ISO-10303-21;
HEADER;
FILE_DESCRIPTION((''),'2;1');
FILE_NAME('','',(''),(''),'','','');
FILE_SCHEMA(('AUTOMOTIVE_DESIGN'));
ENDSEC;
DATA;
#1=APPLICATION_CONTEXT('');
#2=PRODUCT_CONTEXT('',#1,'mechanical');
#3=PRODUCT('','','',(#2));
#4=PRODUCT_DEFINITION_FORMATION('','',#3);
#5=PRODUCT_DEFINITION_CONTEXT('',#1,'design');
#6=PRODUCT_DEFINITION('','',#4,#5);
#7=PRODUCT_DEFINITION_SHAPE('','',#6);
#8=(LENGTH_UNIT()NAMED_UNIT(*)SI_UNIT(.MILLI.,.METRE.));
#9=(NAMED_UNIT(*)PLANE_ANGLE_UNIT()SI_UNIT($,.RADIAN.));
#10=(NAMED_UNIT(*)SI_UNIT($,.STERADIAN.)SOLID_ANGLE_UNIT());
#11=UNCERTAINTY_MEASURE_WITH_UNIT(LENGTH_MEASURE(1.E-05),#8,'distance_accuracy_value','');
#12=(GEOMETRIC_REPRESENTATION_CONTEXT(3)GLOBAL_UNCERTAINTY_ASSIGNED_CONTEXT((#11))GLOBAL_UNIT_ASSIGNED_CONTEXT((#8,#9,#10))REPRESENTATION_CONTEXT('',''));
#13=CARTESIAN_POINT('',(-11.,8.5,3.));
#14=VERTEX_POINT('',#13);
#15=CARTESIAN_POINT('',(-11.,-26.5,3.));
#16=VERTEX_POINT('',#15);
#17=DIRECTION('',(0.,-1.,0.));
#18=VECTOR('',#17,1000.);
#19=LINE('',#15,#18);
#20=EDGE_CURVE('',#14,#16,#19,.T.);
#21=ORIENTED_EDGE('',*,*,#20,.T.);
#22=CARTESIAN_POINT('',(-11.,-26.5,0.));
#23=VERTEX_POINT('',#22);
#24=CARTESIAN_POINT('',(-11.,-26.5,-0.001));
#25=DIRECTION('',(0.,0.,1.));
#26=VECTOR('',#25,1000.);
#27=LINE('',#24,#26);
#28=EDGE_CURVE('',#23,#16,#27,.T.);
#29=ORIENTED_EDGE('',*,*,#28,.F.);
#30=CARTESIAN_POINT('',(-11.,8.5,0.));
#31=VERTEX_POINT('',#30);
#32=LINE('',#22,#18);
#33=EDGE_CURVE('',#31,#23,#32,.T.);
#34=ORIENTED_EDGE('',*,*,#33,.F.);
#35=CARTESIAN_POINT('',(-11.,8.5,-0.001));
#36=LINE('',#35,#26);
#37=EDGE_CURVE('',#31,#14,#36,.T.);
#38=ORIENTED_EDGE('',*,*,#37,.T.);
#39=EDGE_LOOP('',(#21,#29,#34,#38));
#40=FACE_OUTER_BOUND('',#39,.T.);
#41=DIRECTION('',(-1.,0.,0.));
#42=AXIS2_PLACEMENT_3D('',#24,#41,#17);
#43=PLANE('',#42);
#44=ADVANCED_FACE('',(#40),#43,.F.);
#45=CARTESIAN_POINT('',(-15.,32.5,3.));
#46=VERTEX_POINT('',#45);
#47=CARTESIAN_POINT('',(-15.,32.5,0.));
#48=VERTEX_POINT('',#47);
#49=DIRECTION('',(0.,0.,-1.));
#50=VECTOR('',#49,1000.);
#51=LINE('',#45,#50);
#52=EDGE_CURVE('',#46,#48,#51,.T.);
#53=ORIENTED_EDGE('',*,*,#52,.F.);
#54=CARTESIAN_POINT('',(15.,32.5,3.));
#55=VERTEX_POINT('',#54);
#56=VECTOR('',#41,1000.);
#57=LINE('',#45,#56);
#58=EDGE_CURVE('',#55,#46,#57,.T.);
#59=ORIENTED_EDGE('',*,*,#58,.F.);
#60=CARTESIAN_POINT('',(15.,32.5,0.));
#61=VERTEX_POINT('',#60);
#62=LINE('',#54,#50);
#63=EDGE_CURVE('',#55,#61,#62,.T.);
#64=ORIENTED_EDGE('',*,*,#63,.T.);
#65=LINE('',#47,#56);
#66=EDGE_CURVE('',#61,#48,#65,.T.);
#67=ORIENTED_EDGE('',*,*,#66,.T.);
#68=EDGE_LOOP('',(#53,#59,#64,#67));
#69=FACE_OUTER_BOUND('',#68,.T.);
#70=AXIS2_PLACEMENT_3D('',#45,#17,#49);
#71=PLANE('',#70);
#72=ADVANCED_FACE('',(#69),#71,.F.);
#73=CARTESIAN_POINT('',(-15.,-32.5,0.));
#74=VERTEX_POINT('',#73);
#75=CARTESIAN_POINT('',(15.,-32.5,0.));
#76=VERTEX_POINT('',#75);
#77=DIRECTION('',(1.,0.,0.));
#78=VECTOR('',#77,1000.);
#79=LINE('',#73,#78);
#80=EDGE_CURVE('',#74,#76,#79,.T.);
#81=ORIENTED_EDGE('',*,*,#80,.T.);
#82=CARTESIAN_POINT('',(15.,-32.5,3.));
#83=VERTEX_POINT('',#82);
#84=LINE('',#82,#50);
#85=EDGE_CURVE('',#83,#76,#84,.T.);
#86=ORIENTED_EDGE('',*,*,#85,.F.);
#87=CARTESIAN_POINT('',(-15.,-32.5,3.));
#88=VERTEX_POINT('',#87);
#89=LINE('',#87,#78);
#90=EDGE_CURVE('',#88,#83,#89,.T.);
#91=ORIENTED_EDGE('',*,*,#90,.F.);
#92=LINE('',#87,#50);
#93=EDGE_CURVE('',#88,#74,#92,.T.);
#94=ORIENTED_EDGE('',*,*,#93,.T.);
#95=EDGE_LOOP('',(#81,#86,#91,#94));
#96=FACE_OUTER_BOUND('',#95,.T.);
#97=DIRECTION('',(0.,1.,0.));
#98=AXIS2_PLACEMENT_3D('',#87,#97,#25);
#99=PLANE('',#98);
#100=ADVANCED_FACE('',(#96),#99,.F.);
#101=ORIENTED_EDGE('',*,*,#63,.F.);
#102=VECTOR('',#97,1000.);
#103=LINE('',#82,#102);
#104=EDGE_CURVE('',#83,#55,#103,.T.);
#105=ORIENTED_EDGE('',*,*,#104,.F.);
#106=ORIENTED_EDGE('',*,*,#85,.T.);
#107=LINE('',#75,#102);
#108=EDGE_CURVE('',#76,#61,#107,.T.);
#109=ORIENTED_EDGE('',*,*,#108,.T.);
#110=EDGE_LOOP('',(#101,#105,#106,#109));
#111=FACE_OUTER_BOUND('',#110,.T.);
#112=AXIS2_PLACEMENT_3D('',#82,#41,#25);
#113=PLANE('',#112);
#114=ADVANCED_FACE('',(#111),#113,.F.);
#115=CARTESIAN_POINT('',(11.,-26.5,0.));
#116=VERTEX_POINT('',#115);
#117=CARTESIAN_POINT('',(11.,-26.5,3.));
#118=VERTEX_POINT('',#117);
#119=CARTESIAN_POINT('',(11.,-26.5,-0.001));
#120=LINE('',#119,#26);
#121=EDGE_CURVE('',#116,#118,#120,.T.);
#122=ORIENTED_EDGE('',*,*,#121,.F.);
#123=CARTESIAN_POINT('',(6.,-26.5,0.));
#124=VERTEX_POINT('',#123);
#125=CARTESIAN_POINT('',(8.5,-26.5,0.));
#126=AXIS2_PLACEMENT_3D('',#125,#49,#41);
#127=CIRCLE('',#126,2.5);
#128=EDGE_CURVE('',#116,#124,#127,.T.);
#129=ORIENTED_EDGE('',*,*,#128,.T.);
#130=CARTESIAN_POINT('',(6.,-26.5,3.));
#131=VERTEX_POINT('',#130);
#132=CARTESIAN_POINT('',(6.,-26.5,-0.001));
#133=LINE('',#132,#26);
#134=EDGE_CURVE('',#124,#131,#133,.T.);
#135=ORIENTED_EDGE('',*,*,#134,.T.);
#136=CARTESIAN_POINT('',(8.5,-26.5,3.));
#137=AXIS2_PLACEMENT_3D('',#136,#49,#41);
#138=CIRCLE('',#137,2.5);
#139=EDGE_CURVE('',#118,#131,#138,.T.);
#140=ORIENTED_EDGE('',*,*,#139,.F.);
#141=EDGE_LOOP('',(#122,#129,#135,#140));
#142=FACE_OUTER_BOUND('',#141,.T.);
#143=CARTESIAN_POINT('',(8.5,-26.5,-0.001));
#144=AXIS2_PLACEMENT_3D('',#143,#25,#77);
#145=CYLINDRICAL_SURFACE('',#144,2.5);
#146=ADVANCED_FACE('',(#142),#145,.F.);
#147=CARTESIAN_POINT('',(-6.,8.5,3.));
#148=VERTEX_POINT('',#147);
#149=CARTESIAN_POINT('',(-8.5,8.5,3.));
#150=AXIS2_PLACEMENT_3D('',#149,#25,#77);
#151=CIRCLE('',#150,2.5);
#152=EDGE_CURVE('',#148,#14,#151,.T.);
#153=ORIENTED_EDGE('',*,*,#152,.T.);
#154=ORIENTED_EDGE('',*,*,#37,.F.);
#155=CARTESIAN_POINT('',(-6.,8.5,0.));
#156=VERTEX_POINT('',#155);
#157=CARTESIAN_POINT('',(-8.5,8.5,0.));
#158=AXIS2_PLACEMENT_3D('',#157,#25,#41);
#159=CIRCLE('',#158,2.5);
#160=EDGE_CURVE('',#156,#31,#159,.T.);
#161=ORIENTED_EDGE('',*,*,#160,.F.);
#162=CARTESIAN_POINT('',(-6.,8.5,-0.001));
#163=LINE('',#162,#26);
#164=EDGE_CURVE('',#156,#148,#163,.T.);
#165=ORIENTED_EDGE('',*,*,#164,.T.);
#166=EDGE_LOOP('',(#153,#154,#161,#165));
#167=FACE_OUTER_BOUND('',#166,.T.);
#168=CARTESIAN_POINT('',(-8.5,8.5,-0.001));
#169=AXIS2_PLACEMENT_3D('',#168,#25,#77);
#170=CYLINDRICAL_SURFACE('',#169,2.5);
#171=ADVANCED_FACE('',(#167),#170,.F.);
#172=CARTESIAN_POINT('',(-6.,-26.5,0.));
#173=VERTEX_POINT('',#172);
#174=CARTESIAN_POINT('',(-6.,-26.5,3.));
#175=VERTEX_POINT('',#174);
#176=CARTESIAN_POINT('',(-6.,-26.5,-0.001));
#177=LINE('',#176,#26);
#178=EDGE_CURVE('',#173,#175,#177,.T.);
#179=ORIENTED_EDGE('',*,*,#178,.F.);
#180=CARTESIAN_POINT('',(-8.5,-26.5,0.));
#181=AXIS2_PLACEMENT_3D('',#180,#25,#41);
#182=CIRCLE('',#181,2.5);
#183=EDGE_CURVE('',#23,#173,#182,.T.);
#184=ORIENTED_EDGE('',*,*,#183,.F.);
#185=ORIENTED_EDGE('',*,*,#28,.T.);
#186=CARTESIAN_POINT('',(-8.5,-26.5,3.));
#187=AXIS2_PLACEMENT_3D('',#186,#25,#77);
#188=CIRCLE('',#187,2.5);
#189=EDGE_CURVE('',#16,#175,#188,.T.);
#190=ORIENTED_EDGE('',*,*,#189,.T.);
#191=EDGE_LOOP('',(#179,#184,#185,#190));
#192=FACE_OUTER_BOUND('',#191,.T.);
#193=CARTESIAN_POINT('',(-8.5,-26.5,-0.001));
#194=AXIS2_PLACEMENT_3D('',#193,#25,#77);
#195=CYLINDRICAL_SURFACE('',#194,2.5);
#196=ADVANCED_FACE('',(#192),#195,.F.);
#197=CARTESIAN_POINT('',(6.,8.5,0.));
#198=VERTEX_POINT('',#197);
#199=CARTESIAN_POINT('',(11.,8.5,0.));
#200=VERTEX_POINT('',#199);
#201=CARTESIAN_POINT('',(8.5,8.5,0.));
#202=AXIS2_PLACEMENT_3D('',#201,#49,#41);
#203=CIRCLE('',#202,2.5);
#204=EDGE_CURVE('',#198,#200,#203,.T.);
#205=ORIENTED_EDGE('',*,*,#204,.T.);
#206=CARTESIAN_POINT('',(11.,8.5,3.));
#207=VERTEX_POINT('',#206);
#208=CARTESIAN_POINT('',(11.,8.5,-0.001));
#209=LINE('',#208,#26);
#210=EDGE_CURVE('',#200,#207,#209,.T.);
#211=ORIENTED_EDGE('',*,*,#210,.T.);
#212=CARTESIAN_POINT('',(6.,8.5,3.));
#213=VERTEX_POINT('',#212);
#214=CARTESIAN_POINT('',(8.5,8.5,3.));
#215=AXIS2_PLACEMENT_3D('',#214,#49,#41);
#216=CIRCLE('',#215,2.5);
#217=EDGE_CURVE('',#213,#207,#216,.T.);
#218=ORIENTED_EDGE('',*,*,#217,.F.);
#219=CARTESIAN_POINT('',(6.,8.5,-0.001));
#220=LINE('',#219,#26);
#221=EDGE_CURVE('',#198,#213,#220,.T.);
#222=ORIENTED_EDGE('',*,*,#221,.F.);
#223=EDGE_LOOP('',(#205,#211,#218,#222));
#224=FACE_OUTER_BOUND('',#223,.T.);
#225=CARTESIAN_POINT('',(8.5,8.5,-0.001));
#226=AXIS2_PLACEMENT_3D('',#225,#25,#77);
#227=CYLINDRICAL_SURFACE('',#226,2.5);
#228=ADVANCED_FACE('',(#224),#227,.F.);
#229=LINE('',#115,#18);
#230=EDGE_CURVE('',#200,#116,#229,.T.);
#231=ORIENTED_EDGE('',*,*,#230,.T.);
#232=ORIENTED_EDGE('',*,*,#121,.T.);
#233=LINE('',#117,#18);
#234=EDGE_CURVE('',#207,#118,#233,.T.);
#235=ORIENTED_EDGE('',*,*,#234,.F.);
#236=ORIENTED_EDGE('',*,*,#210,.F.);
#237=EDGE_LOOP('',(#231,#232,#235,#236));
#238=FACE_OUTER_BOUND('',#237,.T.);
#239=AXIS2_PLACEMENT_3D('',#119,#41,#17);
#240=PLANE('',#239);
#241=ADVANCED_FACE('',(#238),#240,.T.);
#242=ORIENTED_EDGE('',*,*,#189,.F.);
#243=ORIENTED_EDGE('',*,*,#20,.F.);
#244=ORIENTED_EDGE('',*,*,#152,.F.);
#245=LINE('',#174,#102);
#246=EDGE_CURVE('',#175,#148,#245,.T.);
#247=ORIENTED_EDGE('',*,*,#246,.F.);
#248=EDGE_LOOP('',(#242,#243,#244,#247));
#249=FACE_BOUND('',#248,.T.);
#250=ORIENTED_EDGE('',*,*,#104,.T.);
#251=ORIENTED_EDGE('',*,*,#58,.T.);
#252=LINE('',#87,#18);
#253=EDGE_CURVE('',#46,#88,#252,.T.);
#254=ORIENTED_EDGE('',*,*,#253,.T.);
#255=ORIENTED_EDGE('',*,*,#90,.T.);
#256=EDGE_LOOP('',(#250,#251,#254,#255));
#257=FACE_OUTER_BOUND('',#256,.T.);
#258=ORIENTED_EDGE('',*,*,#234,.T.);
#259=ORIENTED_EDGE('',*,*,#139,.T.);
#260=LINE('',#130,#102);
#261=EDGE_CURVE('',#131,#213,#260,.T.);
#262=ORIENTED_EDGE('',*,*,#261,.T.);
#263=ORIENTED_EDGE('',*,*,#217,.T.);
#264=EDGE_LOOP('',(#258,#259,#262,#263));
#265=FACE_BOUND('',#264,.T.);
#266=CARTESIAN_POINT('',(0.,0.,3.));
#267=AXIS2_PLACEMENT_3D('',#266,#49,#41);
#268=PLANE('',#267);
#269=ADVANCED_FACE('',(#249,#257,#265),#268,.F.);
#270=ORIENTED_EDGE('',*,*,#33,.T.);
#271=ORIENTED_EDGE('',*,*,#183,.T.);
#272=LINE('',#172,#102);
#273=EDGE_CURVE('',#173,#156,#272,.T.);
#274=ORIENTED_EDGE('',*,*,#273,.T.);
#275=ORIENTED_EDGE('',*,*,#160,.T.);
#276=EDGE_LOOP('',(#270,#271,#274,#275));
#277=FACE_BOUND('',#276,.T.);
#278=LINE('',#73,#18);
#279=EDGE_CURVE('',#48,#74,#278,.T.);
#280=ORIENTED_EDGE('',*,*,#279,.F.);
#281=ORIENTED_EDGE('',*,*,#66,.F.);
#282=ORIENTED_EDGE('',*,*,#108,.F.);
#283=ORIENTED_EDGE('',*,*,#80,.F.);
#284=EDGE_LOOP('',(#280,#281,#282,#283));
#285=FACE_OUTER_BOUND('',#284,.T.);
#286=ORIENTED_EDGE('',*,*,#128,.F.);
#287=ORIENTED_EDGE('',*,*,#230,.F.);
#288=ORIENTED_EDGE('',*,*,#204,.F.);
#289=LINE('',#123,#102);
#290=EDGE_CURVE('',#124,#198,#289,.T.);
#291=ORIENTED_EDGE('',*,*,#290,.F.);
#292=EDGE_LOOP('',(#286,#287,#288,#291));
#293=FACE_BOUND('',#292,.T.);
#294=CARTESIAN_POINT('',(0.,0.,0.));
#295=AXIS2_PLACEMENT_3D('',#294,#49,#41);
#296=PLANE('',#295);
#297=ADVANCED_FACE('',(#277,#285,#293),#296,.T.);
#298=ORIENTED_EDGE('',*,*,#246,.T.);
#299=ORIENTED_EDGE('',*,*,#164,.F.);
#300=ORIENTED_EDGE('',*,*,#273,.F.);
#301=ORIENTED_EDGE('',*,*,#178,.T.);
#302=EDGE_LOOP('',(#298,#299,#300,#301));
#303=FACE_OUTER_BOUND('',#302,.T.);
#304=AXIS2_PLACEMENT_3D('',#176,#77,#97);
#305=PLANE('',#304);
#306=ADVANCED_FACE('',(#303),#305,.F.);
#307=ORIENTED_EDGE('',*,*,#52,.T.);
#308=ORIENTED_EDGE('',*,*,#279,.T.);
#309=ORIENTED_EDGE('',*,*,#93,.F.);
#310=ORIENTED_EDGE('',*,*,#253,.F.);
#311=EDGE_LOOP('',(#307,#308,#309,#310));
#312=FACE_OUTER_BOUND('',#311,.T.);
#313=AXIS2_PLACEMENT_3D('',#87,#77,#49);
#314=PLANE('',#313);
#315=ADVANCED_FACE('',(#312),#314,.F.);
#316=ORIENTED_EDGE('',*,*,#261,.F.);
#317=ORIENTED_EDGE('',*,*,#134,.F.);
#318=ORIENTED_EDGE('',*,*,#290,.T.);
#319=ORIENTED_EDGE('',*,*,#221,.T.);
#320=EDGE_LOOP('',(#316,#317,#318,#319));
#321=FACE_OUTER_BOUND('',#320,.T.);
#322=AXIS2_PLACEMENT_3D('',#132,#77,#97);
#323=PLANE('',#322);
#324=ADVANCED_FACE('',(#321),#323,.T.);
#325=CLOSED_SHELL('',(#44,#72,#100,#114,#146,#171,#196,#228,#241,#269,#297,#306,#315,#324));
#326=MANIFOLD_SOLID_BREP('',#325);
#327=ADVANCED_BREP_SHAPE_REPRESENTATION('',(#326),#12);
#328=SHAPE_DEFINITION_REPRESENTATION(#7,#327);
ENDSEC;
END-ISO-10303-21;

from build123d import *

# Parameters (mm, degrees)
SKETCH_1_W          = 30
SKETCH_1_H          = 65
EXTRUDE_1_DEPTH     = 3
CUT_EXTRUDE_1_REACH = 37.92


with BuildPart() as part:
    # 草图1 → 凸台-拉伸1 (new body)
    with BuildSketch(Plane.XY):
        Rectangle(SKETCH_1_W, SKETCH_1_H)
    extrude(amount=EXTRUDE_1_DEPTH)

    # 草图2 → 切除-拉伸1 (cut, up to next)
    with BuildSketch(Plane.XY.offset(3), mode=Mode.PRIVATE) as cut_extrude_1_sk1:
        with BuildLine():
            Line((-11, -26.5), (-11, 8.5))
            ThreePointArc((-11, 8.5), (-8.5, 11), (-6, 8.5))
            Line((-6, 8.5), (-6, -26.5))
            ThreePointArc((-6, -26.5), (-8.5, -29), (-11, -26.5))
        make_face()
    cut_extrude_1_tool1 = extrude(cut_extrude_1_sk1.sketch, amount=-CUT_EXTRUDE_1_REACH, mode=Mode.PRIVATE) & part.part
    cut_extrude_1 = cut_extrude_1_tool1.solids().sort_by_distance((-8.5, -9, 3))[0]
    add(cut_extrude_1, mode=Mode.SUBTRACT)

    # 镜向1: 切除-拉伸1 across plane
    add(cut_extrude_1.mirror(Plane(origin=(0, 0, 0), x_dir=(0, 0, 1), z_dir=(1, 0, 0))), mode=Mode.SUBTRACT)


solid = part.part
